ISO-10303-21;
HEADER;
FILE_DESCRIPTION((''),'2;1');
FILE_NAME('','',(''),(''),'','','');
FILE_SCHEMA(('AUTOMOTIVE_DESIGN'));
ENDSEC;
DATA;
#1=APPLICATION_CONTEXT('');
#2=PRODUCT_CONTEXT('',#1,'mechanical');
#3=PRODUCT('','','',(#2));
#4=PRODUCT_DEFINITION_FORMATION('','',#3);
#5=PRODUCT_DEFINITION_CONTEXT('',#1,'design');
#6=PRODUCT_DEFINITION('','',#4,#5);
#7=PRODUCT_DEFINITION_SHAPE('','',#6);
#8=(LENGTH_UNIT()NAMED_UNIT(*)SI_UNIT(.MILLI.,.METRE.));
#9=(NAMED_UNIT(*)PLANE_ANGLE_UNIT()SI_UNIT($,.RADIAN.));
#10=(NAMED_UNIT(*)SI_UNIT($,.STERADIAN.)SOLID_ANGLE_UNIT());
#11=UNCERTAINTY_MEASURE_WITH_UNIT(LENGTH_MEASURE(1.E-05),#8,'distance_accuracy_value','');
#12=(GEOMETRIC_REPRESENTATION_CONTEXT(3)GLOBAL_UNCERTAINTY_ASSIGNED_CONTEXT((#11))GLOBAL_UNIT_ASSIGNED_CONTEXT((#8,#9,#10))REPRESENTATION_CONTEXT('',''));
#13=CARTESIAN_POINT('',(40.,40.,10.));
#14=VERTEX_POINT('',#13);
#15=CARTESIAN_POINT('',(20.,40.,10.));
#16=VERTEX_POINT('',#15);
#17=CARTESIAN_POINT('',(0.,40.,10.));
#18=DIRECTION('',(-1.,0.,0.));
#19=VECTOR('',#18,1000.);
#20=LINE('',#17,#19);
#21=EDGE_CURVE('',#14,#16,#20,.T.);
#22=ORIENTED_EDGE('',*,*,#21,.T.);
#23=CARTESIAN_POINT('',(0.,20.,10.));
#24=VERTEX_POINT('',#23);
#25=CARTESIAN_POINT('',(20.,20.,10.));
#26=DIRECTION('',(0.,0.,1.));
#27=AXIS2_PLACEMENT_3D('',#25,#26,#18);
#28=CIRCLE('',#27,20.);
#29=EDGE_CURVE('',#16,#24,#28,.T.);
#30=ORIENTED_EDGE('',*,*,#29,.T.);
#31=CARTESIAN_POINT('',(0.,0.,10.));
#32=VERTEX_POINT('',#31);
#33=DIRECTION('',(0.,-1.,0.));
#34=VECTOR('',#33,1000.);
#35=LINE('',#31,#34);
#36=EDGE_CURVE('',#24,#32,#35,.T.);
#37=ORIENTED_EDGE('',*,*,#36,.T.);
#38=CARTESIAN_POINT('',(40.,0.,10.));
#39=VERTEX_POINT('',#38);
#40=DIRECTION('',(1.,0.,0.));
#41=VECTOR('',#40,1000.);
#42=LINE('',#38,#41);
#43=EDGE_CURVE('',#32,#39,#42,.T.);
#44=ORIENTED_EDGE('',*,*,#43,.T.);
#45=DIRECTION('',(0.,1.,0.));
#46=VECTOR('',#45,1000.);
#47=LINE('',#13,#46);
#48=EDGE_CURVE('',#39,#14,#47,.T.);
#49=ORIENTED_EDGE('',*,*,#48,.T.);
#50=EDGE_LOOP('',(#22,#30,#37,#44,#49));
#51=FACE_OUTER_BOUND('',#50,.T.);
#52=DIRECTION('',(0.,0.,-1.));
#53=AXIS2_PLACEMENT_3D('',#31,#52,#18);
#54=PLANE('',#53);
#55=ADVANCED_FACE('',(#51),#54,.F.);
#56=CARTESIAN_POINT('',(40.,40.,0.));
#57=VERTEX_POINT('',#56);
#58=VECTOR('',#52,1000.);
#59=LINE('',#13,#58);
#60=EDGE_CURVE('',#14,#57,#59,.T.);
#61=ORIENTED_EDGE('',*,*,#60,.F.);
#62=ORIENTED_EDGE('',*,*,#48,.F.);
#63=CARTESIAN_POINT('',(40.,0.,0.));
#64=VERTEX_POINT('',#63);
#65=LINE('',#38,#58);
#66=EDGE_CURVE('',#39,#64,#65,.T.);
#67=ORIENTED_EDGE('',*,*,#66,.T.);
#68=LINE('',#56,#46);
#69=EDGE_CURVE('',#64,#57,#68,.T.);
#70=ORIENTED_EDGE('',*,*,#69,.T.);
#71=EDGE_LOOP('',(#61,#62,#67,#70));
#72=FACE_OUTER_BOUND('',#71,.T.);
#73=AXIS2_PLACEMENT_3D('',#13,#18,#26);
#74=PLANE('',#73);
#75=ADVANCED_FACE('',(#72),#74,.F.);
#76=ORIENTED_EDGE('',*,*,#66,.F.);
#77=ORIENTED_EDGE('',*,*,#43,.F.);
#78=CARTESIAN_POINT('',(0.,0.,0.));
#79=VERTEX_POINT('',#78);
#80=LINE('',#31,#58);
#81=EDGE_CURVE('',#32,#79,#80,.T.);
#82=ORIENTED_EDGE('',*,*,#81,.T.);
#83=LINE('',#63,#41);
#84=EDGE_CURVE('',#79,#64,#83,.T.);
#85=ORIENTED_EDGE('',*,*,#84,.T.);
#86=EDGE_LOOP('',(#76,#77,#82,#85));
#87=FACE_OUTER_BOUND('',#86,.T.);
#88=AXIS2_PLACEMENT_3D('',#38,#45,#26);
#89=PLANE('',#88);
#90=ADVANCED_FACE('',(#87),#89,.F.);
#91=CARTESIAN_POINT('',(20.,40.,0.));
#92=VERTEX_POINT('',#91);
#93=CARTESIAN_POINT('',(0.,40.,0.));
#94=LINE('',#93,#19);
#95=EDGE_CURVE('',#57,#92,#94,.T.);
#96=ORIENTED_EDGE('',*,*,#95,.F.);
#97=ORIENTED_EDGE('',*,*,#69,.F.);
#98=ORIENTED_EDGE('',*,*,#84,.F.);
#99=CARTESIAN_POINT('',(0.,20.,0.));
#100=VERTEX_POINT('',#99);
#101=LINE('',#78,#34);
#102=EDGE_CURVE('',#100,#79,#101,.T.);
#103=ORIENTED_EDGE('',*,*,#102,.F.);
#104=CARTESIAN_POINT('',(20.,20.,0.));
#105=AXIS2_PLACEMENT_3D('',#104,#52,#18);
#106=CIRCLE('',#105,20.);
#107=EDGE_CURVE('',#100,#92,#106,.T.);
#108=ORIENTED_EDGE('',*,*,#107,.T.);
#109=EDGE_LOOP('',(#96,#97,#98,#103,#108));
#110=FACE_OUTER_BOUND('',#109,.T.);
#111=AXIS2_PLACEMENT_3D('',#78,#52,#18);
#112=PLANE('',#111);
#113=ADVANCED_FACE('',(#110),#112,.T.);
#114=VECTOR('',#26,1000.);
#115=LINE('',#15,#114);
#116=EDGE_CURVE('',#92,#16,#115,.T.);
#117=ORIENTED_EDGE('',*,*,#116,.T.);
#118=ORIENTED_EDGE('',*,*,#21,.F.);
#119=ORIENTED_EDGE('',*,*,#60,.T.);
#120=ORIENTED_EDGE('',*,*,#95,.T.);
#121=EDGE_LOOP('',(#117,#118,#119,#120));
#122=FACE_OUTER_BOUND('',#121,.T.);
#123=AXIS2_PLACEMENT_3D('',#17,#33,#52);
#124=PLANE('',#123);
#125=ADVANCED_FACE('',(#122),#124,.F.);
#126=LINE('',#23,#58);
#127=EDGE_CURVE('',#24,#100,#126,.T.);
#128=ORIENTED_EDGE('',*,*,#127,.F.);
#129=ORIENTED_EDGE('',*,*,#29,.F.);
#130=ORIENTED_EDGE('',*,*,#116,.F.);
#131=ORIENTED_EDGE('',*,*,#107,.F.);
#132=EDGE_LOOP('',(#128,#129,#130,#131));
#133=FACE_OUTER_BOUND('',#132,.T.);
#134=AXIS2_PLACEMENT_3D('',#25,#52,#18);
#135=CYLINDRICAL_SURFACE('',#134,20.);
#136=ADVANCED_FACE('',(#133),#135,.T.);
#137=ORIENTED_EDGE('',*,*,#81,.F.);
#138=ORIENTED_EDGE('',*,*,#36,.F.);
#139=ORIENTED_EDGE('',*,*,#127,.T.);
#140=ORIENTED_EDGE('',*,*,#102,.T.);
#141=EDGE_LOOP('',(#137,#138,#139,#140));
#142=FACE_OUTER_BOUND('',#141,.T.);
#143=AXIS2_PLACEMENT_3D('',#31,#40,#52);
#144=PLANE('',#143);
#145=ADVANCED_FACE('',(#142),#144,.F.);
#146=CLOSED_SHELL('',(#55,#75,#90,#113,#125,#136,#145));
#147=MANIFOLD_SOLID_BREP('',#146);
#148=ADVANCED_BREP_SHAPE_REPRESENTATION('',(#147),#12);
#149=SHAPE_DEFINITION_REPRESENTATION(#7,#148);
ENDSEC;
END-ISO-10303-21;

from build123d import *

# Parameters (mm, degrees)
SKETCH1_W           = 40
SKETCH1_H           = 40
BOSS_EXTRUDE1_DEPTH = 10
FILLET1_R           = 20


with BuildPart() as part:
    # Sketch1 → Boss-Extrude1 (new body)
    with BuildSketch(Plane.XY):
        with Locations((20, 20)):
            Rectangle(SKETCH1_W, SKETCH1_H)
    extrude(amount=BOSS_EXTRUDE1_DEPTH)

    # Fillet1
    fillet1_edges = [part.edges().sort_by_distance(p)[0] for p in [
        (0, 40, 5),
    ]]
    fillet(fillet1_edges, radius=FILLET1_R)


solid = part.part
